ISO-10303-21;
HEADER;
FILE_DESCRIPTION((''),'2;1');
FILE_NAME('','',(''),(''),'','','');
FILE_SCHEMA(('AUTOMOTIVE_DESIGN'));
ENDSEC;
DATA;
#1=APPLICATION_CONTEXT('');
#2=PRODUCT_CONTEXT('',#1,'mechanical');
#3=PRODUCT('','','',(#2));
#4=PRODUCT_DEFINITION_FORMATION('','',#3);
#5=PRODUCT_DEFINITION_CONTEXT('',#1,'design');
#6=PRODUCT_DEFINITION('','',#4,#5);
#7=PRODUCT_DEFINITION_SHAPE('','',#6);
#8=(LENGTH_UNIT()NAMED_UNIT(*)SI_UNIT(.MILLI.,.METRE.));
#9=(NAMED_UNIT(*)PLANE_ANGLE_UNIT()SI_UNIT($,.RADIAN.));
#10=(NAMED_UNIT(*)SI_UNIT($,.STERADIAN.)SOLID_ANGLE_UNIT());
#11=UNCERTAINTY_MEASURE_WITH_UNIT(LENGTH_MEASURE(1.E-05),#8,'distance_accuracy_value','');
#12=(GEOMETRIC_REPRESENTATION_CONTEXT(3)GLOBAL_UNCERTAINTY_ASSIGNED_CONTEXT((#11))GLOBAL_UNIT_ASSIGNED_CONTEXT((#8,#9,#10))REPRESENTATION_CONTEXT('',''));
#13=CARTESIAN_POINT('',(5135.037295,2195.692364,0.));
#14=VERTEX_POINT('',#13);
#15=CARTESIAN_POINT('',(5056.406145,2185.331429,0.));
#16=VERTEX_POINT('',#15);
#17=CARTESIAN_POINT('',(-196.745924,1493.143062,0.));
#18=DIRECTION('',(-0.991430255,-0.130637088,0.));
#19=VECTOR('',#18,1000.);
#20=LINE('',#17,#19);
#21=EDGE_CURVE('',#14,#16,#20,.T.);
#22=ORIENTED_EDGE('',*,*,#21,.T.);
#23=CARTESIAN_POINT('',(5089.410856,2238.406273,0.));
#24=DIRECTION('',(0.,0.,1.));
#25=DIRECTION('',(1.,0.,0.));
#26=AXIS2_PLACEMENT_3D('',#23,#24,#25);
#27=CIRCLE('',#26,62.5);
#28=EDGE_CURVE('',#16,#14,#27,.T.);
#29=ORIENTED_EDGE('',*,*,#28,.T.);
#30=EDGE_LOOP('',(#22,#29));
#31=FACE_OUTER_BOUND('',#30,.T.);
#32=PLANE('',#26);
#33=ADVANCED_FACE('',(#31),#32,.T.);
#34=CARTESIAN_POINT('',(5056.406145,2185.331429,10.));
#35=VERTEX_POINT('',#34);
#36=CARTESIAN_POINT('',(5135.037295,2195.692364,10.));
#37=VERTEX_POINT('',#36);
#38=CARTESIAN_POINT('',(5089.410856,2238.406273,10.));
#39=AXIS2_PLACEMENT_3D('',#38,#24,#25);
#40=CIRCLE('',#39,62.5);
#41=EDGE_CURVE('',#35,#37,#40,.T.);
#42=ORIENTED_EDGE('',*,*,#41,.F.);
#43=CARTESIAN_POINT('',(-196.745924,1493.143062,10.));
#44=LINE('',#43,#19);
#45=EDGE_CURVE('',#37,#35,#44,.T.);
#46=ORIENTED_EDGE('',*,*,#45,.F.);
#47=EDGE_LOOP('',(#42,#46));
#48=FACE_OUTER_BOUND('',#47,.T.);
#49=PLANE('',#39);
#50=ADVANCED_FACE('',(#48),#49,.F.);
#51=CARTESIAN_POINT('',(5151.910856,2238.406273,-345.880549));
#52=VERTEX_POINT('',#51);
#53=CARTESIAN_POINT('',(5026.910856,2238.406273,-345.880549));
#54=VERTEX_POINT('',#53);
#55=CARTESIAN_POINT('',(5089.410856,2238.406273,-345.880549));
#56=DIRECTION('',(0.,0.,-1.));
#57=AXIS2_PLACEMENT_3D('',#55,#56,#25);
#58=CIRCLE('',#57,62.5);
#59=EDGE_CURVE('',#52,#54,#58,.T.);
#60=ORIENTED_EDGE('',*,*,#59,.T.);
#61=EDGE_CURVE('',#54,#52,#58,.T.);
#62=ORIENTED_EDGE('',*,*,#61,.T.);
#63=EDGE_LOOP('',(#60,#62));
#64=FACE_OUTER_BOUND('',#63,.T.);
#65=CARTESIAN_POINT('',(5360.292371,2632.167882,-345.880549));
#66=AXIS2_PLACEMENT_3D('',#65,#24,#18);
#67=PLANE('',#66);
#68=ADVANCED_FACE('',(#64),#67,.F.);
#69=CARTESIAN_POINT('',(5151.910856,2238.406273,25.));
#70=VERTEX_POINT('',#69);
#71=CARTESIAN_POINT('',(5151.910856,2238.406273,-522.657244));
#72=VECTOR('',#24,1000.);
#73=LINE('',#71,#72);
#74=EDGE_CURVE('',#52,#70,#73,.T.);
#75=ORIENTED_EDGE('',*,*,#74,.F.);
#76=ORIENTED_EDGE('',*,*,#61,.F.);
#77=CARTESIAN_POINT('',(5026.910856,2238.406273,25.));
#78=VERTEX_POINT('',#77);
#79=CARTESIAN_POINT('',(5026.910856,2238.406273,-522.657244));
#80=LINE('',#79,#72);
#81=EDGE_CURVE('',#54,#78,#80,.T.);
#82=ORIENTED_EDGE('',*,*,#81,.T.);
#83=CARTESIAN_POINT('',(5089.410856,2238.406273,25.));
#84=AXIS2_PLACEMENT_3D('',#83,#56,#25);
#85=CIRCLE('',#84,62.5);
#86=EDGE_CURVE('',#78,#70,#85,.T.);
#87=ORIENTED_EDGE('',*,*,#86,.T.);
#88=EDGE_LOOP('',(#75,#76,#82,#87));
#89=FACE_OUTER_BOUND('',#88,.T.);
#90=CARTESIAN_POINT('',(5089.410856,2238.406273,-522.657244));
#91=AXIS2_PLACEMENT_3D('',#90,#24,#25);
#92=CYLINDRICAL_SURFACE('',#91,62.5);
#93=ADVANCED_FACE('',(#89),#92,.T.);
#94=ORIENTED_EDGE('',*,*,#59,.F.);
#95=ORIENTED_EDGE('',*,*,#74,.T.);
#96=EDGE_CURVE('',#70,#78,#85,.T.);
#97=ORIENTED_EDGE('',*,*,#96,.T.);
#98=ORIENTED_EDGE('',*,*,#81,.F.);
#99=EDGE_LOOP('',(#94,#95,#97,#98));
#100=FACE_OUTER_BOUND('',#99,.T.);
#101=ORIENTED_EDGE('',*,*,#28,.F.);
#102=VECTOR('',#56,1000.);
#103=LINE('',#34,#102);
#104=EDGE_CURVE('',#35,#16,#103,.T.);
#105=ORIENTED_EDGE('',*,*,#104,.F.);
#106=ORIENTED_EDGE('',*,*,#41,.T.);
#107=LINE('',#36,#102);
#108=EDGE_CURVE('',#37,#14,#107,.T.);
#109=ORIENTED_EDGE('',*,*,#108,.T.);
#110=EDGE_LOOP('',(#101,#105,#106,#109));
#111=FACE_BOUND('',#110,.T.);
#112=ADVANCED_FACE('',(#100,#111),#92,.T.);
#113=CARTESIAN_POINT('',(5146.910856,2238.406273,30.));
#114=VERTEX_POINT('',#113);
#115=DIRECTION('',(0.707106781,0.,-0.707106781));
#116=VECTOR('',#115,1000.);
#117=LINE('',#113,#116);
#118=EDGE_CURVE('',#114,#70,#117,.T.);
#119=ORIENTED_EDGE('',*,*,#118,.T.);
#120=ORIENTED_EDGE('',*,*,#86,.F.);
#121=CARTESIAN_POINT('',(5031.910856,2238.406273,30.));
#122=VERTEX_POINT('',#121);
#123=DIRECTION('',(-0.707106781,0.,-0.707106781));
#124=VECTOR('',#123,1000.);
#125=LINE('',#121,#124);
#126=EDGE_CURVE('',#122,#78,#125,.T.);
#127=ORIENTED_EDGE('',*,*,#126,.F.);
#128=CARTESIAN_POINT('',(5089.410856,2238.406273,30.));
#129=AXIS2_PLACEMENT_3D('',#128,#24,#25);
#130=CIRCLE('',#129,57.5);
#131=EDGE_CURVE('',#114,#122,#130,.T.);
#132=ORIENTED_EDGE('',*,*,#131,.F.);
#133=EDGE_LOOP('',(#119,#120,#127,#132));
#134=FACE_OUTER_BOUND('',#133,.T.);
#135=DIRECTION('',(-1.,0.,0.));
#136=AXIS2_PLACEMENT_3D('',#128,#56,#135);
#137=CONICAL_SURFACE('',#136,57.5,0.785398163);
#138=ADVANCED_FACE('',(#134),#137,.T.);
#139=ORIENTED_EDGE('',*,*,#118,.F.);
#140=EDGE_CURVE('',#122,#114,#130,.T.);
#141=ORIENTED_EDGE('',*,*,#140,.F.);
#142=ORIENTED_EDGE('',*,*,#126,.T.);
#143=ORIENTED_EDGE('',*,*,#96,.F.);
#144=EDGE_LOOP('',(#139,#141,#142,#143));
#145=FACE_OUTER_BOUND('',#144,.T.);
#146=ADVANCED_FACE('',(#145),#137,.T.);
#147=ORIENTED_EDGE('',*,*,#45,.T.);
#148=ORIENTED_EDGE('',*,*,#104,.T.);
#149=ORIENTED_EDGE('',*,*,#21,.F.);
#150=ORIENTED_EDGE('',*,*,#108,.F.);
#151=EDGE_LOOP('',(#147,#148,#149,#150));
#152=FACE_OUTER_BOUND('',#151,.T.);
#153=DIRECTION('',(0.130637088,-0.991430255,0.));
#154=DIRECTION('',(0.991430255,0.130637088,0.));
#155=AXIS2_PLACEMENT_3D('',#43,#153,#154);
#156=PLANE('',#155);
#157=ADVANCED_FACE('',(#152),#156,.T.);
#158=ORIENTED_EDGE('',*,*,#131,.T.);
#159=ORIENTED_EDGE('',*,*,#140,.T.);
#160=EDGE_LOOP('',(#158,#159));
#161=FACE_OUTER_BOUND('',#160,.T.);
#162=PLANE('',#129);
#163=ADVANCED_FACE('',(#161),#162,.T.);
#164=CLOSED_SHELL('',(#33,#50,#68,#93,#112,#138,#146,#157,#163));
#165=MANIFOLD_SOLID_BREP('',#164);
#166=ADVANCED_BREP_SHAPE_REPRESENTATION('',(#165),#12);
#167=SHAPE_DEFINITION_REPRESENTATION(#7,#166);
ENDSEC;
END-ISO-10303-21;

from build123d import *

# Parameters (mm, degrees)
SKETCH1_R           = 62.5
BOSS_EXTRUDE1_DEPTH = 345.880548662
BOSS_EXTRUDE2_START = 10
BOSS_EXTRUDE2_DEPTH = 10
BOSS_EXTRUDE3_START = 20
SKETCH4_R           = 62.5
BOSS_EXTRUDE3_DEPTH = 20
CHAMFER1_SIZE       = 5


with BuildPart() as part:
    # Sketch1 → Boss-Extrude1 (new body)
    with BuildSketch(Plane.XY):
        with Locations((5089.410855653, 2238.406272837)):
            Circle(SKETCH1_R)
    extrude(amount=-BOSS_EXTRUDE1_DEPTH)

    # Sketch3 → Boss-Extrude2 (add)
    with BuildSketch(Plane.XY.offset(BOSS_EXTRUDE2_START)):
        with BuildLine():
            Line((5056.406144678, 2185.331428951), (5095.721720008, 2190.511896514))
            Line((5095.721720008, 2190.511896514), (5135.037295338, 2195.692364076))
            ThreePointArc((5135.037295338, 2195.692364076), (5147.539602759, 2215.443286101), (5151.910855653, 2238.406272837))
            ThreePointArc((5151.910855653, 2238.406272837), (5059.050885593, 2293.037053702), (5056.406144678, 2185.331428951))
        make_face()
    extrude(amount=-BOSS_EXTRUDE2_DEPTH)

    # Sketch4 → Boss-Extrude3 (add)
    with BuildSketch(Plane.XY.offset(10).offset(BOSS_EXTRUDE3_START)):
        with Locations((5089.410855653, 2238.406272837)):
            Circle(SKETCH4_R)
    extrude(amount=-BOSS_EXTRUDE3_DEPTH)

    # Chamfer1
    chamfer1_edges = [part.edges().sort_by_distance(p)[0] for p in [
        (5026.910855653, 2238.406272837, 30),
    ]]
    chamfer(chamfer1_edges, length=CHAMFER1_SIZE)


solid = part.part
